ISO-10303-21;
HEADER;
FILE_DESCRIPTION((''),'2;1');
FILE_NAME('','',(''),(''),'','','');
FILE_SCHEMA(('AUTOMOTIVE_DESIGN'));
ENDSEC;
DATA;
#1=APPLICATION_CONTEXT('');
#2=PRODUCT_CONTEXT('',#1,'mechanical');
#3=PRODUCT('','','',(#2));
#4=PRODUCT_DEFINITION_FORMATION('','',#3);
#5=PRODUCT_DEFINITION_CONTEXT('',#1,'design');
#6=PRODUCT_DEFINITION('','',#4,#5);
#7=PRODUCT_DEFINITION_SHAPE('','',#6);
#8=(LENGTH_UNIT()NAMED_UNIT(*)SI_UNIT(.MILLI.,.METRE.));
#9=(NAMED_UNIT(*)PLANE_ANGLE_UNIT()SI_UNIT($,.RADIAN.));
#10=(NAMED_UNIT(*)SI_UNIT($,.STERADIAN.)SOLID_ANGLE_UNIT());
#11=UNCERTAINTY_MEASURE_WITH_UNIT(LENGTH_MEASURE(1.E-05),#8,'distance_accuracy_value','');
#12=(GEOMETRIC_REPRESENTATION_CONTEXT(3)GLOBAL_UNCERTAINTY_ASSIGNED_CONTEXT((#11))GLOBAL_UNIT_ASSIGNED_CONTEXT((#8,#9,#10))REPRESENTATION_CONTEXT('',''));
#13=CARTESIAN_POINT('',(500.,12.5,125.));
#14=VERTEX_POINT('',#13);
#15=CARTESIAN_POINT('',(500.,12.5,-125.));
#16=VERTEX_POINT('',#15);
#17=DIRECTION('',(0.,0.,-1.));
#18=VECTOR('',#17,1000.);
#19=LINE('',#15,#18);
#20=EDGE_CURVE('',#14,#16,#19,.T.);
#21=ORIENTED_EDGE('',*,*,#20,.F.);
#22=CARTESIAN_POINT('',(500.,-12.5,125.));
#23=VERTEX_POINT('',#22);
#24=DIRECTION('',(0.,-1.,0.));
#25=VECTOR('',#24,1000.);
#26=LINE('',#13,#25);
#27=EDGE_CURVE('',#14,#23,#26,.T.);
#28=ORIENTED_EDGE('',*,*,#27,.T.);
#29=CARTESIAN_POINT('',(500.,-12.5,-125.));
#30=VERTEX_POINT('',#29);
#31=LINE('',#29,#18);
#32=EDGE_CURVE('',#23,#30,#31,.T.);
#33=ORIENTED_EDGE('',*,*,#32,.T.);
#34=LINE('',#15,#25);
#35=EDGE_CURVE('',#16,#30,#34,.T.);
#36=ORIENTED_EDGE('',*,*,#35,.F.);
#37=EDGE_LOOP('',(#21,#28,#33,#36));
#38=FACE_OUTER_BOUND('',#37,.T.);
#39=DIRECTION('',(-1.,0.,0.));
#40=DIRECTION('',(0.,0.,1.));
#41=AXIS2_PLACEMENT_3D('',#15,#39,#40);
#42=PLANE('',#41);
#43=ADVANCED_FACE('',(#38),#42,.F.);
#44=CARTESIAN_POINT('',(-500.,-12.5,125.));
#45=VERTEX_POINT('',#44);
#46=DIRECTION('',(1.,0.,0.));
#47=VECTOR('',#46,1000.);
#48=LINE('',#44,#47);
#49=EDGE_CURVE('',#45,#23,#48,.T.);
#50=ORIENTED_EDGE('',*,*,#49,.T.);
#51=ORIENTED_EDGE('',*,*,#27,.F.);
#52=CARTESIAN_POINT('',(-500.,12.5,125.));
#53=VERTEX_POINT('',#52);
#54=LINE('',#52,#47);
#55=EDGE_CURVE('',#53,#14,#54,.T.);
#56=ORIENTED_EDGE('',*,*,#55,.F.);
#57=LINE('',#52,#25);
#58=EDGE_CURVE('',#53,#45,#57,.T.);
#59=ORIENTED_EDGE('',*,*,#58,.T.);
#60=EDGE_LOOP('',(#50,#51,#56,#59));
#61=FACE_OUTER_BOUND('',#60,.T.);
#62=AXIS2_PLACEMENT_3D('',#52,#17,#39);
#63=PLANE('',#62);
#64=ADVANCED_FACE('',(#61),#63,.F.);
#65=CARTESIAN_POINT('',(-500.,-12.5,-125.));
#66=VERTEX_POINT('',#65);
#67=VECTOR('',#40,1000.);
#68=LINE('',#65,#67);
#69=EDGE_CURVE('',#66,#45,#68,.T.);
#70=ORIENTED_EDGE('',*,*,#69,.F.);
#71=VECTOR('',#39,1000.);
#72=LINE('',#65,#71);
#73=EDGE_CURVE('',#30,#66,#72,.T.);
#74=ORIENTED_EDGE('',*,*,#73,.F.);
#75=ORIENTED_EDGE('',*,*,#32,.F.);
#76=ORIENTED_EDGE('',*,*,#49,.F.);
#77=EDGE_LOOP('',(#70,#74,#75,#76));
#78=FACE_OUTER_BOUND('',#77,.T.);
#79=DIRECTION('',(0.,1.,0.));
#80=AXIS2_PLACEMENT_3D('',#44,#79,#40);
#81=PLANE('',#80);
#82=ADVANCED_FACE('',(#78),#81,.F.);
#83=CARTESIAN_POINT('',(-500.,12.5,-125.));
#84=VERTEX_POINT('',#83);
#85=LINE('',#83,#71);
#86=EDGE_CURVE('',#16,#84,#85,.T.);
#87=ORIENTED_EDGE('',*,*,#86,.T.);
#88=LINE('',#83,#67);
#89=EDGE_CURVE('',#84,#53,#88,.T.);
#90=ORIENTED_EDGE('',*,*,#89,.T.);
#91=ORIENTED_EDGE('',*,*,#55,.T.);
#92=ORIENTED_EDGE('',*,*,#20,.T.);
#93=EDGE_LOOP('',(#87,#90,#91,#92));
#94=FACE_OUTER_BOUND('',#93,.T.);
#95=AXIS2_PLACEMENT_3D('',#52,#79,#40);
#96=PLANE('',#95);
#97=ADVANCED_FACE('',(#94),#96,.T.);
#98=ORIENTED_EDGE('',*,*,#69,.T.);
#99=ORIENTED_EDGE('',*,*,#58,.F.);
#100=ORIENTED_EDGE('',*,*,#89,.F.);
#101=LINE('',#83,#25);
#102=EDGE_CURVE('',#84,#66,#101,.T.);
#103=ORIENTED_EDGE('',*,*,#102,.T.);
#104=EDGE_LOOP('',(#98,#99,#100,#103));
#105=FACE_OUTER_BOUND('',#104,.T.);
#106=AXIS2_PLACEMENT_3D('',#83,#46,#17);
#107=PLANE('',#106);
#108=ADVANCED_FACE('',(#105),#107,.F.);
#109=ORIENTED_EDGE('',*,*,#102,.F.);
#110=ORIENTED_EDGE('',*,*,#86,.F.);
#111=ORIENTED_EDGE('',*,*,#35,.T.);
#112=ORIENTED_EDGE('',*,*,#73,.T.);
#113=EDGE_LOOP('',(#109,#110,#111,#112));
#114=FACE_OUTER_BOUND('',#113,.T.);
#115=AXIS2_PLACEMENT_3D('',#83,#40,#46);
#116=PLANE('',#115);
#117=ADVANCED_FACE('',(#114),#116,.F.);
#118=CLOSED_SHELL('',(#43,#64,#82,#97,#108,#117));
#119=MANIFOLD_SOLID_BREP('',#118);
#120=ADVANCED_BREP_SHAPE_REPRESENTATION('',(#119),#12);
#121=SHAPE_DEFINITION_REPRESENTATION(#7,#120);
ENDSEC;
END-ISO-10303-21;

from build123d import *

# Parameters (mm, degrees)
SKETCH1_W      = 1000
SKETCH1_H      = 250
EXTRUDE1_DEPTH = 12.5


with BuildPart() as part:
    # Sketch1 → Extrude1 (new, symmetric)
    with BuildSketch(Plane(origin=(0, 0, 0), x_dir=(1, 0, 0), z_dir=(0, 1, 0))):
        Rectangle(SKETCH1_W, SKETCH1_H)
    extrude(amount=EXTRUDE1_DEPTH, both=True)


solid = part.part
